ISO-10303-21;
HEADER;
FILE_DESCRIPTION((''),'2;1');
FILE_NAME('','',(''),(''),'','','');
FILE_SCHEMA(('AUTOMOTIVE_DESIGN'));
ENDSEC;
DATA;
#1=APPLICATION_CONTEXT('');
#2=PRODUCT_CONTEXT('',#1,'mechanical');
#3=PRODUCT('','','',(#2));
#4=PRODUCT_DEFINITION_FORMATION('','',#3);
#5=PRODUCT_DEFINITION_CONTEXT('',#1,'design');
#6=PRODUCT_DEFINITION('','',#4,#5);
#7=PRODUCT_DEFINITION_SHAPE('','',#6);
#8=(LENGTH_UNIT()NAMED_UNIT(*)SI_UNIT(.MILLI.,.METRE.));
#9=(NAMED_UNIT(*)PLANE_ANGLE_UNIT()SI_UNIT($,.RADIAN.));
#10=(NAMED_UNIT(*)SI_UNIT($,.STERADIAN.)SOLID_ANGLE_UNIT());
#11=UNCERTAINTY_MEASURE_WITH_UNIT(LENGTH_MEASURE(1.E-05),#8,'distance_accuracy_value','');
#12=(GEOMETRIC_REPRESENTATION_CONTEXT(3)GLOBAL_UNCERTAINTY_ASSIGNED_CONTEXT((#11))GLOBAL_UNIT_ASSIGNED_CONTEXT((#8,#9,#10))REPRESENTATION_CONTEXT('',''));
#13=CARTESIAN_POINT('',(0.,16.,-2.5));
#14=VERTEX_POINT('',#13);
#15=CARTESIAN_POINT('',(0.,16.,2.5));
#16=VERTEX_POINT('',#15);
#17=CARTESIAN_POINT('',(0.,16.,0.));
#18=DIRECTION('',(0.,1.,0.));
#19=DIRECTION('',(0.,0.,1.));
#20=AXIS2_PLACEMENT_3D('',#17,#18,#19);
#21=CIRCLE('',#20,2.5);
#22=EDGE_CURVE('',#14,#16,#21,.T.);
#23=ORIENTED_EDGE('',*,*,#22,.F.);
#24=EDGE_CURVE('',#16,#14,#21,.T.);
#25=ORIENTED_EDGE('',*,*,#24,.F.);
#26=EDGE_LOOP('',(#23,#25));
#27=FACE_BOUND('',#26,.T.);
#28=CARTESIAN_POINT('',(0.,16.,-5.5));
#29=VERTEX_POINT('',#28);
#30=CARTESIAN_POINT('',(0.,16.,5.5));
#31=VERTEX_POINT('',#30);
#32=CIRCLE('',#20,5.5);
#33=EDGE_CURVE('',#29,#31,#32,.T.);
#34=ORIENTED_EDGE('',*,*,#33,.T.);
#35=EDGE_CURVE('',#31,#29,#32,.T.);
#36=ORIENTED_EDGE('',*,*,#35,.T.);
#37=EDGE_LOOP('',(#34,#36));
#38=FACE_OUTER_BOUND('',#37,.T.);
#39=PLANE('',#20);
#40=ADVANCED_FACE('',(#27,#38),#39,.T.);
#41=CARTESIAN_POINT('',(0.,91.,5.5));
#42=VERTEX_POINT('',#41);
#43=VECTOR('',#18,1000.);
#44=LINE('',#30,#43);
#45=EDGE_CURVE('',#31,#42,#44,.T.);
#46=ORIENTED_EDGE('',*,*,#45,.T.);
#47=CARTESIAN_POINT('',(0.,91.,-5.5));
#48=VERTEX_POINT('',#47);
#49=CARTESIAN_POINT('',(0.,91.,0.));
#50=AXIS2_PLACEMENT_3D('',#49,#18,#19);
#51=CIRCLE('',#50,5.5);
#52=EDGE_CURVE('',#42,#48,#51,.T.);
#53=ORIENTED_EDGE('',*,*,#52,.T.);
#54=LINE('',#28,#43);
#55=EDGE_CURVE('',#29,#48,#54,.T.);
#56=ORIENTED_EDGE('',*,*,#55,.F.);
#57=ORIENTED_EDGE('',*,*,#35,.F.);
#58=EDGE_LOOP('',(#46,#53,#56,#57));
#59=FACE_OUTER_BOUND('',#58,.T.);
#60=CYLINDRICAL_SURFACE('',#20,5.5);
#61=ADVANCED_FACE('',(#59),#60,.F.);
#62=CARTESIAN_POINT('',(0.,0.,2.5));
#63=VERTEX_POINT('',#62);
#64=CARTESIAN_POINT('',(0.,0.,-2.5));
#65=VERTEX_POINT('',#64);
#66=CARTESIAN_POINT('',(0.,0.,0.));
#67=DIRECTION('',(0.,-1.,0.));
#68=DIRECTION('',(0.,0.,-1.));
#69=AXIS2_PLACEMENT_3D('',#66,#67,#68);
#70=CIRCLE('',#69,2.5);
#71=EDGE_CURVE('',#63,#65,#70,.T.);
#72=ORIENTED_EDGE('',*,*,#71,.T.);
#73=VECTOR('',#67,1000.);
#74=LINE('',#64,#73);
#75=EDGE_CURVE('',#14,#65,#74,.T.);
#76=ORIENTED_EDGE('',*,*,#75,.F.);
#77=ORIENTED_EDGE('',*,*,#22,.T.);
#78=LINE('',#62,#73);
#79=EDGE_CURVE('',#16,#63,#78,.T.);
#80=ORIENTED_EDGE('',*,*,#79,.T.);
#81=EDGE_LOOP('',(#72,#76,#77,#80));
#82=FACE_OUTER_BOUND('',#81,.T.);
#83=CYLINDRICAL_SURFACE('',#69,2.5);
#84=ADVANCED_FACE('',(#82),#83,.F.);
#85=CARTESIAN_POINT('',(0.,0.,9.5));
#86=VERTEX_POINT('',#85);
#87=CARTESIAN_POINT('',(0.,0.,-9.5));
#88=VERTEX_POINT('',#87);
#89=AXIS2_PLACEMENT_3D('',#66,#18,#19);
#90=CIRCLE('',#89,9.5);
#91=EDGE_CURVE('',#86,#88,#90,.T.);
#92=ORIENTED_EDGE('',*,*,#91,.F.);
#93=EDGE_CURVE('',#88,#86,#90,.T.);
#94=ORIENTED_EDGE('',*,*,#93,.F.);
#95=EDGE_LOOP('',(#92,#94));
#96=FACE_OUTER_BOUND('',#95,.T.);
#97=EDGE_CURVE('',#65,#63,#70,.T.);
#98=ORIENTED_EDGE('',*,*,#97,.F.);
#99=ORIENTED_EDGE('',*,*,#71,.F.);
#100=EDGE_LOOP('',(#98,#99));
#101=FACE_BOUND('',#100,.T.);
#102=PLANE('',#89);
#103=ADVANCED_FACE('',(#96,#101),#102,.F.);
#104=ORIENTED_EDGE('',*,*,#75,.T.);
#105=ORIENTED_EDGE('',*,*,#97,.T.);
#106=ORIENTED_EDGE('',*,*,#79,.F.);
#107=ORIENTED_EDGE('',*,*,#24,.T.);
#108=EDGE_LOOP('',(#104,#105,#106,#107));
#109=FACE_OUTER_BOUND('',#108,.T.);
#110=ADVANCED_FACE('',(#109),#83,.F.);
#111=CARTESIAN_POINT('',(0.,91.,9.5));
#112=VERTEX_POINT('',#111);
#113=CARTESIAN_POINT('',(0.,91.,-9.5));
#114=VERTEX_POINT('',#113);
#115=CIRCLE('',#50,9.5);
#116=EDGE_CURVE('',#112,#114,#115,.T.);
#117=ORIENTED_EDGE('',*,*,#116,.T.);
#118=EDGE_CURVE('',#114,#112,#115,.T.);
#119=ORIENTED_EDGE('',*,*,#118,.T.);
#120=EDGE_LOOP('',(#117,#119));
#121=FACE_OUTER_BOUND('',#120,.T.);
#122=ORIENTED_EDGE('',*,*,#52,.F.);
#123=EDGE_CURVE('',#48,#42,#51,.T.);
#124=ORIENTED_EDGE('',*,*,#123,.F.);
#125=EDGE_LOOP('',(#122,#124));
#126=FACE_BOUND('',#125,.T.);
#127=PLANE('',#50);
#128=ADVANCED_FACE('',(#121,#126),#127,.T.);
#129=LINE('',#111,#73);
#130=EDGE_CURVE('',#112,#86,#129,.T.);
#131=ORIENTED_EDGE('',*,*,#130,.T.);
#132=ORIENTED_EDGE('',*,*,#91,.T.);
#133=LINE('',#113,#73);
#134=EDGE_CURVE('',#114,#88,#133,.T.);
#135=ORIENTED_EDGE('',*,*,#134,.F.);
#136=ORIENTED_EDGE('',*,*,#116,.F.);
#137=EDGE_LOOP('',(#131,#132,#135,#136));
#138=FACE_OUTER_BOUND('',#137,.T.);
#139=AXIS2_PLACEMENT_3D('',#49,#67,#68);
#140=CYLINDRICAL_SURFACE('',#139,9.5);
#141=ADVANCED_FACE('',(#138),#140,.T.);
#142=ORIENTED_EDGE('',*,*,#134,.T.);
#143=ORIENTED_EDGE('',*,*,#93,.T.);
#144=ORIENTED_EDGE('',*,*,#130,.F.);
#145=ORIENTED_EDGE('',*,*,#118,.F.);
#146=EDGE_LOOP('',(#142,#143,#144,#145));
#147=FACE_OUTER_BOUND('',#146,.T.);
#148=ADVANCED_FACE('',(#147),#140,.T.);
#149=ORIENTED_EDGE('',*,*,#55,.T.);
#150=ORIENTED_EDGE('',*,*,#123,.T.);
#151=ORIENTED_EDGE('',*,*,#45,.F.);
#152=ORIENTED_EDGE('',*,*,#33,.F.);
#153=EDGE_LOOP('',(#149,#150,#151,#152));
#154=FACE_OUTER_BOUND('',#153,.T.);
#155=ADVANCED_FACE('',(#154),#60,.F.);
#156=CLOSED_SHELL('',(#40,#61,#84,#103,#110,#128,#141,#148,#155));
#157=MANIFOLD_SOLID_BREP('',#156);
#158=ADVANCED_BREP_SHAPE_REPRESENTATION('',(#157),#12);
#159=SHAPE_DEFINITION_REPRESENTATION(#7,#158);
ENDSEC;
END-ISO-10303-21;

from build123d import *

# Parameters (mm, degrees)
SKETCH_1_R          = 9.5
EXTRUDE_1_DEPTH     = 91
SKETCH_2_R          = 5.5
CUT_EXTRUDE_1_DEPTH = 75
HOLE_WIZARD_M6_1_D  = 5


with BuildPart() as part:
    # 草图1 → 凸台-拉伸1 (new body)
    with BuildSketch(Plane(origin=(0, 0, 0), x_dir=(1, 0, 0), z_dir=(0, 1, 0))):
        with Locations(Location((0, 0, 0), (0, 0, 270))):
            Circle(SKETCH_1_R)
    extrude(amount=EXTRUDE_1_DEPTH)

    # 草图2 → 切除-拉伸1 (cut)
    with BuildSketch(Plane(origin=(0, 91, 0), x_dir=(1, 0, 0), z_dir=(0, 1, 0))):
        with Locations(Location((0, 0, 0), (0, 0, 270))):
            Circle(SKETCH_2_R)
    extrude(amount=-CUT_EXTRUDE_1_DEPTH, mode=Mode.SUBTRACT)

    # M6 螺纹孔1 (through all)
    with Locations(Plane.XZ):
        with Locations((0, 0)):
            Hole(HOLE_WIZARD_M6_1_D / 2)


solid = part.part
